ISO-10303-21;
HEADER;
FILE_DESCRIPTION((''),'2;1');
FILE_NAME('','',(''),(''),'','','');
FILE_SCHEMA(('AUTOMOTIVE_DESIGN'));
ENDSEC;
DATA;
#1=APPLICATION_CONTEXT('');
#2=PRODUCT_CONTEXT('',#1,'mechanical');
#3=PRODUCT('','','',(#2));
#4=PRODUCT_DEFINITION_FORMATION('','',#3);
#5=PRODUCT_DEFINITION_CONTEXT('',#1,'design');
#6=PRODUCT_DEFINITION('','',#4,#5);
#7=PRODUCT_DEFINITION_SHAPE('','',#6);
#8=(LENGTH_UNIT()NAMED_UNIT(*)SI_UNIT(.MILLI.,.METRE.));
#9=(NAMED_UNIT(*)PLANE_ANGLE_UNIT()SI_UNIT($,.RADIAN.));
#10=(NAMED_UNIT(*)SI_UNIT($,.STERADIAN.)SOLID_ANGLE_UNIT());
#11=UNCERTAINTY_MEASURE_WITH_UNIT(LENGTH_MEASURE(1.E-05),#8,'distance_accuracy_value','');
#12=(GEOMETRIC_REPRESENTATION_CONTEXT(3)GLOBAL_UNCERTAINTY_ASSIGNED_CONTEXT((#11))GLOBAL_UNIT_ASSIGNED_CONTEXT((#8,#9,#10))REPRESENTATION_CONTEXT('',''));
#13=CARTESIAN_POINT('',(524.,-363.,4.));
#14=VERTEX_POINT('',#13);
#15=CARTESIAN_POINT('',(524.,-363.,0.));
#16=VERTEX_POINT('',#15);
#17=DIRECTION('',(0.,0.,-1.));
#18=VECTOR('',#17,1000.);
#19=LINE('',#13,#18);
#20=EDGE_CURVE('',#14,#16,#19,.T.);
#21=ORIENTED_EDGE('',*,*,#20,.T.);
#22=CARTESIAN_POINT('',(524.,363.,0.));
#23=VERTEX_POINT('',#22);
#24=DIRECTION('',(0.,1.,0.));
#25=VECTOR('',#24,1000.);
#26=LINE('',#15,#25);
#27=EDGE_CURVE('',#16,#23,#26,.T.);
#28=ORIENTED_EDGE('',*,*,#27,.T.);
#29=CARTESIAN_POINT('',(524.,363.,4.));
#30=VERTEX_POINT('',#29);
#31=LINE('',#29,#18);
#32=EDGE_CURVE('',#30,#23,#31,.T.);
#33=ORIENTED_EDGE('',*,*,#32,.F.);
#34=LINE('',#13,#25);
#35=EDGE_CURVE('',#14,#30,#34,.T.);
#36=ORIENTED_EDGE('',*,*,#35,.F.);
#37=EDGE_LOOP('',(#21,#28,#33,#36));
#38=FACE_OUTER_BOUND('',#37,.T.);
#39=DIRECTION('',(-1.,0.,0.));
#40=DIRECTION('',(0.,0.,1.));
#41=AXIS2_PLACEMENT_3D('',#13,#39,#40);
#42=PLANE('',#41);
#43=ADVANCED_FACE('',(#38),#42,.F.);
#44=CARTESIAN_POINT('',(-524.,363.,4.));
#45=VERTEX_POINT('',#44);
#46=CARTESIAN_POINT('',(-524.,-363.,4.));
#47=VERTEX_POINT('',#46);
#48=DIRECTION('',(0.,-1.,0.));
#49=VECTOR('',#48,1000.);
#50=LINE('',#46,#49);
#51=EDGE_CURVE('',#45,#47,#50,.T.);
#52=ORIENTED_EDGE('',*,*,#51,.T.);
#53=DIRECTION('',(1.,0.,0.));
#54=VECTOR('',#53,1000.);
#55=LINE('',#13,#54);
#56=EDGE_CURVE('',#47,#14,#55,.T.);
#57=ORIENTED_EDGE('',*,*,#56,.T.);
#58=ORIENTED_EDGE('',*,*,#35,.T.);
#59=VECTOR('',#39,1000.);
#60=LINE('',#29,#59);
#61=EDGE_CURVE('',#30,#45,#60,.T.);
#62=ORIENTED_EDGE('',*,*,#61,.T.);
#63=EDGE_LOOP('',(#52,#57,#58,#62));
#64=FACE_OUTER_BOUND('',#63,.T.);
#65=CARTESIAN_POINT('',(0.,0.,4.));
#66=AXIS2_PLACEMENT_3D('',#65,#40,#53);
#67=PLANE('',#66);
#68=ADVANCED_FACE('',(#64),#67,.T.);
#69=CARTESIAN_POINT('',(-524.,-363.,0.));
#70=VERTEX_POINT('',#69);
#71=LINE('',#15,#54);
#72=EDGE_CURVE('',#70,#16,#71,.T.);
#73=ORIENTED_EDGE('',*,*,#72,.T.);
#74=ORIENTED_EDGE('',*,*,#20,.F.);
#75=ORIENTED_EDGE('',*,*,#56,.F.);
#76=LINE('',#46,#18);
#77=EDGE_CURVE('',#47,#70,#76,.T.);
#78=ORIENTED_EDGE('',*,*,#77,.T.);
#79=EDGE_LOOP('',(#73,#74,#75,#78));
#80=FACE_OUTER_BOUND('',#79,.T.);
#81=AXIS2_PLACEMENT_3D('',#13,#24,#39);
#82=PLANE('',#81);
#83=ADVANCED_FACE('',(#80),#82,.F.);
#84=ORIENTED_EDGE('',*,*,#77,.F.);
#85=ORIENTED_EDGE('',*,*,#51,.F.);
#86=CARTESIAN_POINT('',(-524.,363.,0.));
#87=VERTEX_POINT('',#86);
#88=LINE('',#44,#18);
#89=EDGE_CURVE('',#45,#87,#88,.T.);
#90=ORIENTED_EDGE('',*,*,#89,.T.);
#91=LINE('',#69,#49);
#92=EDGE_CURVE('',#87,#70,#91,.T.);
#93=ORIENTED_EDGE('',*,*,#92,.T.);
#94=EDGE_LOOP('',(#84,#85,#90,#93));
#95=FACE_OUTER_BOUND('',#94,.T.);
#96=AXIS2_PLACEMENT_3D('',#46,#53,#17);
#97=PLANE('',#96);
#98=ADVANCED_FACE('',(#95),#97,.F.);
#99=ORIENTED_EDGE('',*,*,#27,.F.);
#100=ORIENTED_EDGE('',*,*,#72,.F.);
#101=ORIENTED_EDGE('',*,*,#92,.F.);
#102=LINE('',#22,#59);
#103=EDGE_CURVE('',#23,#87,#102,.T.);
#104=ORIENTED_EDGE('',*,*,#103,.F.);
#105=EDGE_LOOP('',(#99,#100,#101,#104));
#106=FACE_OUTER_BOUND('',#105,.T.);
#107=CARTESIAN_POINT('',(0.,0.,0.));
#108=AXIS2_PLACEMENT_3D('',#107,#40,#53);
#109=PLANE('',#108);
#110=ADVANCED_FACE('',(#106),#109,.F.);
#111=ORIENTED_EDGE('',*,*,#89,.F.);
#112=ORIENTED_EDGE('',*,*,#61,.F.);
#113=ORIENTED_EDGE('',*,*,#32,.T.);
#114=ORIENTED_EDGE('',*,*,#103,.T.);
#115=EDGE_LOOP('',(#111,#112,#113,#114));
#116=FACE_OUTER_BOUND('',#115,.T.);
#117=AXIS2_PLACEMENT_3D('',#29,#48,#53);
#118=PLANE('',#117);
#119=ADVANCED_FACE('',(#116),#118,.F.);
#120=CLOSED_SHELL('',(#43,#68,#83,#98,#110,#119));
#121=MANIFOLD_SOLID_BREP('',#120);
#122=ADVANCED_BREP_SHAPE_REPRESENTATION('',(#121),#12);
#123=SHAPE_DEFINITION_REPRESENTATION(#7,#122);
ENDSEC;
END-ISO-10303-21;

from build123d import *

# Parameters (mm, degrees)
SKETCH_1_W      = 1048
SKETCH_1_H      = 726
EXTRUDE_1_DEPTH = 4


with BuildPart() as part:
    # 草图1 → 凸台-拉伸1 (new body)
    with BuildSketch(Plane.XY):
        Rectangle(SKETCH_1_W, SKETCH_1_H)
    extrude(amount=EXTRUDE_1_DEPTH)


solid = part.part
